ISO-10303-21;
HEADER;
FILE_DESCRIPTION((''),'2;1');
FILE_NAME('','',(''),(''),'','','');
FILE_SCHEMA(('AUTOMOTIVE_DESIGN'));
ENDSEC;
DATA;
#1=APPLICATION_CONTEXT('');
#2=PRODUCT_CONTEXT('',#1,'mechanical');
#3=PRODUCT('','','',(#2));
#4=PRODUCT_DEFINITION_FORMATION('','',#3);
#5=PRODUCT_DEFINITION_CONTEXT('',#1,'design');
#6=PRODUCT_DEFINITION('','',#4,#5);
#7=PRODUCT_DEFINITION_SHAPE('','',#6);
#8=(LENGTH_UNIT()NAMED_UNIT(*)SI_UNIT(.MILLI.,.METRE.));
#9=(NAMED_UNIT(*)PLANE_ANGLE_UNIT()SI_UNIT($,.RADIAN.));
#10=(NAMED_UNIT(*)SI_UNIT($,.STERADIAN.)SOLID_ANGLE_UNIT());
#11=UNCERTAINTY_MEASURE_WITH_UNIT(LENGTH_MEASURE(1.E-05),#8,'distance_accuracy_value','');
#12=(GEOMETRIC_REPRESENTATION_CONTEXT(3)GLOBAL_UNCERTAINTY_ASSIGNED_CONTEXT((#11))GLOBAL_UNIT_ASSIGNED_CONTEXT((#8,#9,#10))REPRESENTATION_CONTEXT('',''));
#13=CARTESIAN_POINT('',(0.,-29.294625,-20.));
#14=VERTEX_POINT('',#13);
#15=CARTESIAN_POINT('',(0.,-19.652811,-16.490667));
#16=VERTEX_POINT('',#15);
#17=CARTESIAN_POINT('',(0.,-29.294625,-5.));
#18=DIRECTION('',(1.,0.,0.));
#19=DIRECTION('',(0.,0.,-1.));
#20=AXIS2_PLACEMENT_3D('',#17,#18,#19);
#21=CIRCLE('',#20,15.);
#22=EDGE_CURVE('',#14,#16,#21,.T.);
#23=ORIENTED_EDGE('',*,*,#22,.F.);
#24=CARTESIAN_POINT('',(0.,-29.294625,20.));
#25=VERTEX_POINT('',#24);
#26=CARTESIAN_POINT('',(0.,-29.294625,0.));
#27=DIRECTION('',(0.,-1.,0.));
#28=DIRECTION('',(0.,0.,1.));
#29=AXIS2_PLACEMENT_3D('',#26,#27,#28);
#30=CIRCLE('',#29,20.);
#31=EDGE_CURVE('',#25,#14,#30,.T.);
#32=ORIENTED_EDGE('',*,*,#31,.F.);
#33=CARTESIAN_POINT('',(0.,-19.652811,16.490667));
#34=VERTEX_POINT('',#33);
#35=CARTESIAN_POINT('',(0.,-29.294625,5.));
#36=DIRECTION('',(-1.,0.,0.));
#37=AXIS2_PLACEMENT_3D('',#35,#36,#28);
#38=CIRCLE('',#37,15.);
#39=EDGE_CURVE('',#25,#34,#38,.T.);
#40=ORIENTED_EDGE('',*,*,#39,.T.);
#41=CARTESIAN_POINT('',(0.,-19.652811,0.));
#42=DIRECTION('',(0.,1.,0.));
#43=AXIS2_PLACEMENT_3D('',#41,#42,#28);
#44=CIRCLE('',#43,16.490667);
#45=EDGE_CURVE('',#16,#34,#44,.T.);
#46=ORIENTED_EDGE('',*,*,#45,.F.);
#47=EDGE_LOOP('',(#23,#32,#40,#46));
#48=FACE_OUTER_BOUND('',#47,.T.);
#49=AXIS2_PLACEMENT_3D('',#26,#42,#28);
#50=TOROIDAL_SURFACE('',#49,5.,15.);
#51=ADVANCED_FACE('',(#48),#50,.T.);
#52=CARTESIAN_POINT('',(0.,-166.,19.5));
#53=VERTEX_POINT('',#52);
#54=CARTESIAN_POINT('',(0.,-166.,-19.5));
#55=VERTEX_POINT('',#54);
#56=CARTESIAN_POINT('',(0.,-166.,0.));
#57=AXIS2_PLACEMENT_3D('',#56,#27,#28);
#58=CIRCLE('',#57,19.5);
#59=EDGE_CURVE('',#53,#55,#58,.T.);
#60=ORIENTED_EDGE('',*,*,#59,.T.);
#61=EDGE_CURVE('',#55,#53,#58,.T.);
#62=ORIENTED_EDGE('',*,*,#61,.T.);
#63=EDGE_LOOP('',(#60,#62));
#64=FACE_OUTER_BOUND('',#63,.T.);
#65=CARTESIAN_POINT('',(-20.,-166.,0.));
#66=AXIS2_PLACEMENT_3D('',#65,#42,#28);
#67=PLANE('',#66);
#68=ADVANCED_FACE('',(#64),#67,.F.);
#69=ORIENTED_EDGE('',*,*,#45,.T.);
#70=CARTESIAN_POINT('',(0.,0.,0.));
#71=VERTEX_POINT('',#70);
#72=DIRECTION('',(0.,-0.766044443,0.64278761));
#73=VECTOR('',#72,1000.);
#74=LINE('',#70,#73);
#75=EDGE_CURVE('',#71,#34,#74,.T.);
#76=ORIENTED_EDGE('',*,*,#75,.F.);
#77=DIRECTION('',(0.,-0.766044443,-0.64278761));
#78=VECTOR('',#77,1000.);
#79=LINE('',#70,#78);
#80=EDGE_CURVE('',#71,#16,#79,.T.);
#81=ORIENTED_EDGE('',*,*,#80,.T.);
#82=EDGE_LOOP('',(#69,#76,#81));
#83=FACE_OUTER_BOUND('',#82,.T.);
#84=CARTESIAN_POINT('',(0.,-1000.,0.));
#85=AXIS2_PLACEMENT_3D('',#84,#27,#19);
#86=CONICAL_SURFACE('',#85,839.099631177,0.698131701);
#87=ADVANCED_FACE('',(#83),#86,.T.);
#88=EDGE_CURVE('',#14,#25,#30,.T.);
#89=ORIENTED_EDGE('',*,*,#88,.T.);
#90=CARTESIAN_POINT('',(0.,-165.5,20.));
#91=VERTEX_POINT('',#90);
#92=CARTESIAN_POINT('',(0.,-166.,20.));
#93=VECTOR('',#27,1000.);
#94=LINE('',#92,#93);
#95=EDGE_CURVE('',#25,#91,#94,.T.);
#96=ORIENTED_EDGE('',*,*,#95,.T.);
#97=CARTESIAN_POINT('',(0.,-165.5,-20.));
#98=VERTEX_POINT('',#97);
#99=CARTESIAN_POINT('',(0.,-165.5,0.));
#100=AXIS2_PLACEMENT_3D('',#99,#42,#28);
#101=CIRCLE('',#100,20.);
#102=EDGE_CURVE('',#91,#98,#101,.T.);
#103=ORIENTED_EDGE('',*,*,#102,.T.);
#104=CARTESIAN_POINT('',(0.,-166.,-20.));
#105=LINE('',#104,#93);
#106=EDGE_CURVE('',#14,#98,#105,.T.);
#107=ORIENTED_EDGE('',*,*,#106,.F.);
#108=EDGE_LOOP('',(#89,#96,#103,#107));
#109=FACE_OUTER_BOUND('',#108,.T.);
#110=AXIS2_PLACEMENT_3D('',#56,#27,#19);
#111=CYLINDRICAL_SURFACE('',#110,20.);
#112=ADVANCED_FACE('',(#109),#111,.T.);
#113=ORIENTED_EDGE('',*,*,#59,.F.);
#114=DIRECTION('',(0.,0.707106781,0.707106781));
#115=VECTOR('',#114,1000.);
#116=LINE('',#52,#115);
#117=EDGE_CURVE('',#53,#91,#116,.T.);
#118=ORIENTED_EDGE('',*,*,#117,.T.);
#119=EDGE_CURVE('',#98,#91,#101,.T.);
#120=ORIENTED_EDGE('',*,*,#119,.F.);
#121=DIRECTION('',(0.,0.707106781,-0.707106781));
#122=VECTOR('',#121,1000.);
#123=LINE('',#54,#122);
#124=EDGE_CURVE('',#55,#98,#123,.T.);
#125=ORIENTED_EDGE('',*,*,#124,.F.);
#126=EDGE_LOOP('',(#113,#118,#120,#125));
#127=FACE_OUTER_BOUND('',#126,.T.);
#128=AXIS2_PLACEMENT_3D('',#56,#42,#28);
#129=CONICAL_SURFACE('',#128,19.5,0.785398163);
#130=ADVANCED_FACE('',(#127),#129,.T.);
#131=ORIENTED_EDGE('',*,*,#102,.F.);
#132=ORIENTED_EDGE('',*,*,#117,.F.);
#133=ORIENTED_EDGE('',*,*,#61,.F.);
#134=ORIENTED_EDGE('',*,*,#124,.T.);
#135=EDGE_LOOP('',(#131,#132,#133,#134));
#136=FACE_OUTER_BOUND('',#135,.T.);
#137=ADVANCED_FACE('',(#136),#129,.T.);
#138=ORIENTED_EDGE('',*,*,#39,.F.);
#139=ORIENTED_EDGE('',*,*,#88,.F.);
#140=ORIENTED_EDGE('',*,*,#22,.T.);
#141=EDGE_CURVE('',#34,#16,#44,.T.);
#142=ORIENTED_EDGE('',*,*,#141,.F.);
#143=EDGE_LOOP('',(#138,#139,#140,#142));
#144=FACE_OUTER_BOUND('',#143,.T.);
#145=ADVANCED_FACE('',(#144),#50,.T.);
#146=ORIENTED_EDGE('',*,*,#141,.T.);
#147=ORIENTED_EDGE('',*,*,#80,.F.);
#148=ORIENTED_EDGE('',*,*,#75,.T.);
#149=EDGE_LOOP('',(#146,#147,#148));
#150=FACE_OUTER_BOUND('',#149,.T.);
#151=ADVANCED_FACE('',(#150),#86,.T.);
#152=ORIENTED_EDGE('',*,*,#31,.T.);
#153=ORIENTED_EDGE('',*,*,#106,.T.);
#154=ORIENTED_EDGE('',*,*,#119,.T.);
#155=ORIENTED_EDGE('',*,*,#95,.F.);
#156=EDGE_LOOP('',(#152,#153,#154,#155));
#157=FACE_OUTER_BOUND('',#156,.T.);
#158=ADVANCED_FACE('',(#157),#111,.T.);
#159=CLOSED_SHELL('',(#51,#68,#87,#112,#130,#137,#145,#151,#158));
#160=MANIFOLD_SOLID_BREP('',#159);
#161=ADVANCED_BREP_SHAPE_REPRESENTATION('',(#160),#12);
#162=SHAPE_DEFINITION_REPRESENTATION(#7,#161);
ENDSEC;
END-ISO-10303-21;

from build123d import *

# Parameters (mm, degrees)
FILLET1_R     = 15
CHAMFER1_SIZE = 0.5


with BuildPart() as part:
    # Sketch1 → Revolve1 (revolve)
    with BuildSketch(Plane.XY, mode=Mode.PRIVATE) as revolve1_sk:
        Polygon((0, 0), (-20, -23.835071852), (-20, -166), (0, -166), align=None)
    revolve(revolve1_sk.sketch.rotate(Axis((0, -166, 0), (0, 1, 0)), 270), axis=Axis((0, -166, 0), (0, 1, 0)))

    # Fillet1
    fillet1_edges = [part.edges().sort_by_distance(p)[0] for p in [
        (0, -23.835071852, 20),
    ]]
    fillet(fillet1_edges, radius=FILLET1_R)

    # Chamfer1
    chamfer1_edges = [part.edges().sort_by_distance(p)[0] for p in [
        (0, -166, 20),
    ]]
    chamfer(chamfer1_edges, length=CHAMFER1_SIZE)


solid = part.part
